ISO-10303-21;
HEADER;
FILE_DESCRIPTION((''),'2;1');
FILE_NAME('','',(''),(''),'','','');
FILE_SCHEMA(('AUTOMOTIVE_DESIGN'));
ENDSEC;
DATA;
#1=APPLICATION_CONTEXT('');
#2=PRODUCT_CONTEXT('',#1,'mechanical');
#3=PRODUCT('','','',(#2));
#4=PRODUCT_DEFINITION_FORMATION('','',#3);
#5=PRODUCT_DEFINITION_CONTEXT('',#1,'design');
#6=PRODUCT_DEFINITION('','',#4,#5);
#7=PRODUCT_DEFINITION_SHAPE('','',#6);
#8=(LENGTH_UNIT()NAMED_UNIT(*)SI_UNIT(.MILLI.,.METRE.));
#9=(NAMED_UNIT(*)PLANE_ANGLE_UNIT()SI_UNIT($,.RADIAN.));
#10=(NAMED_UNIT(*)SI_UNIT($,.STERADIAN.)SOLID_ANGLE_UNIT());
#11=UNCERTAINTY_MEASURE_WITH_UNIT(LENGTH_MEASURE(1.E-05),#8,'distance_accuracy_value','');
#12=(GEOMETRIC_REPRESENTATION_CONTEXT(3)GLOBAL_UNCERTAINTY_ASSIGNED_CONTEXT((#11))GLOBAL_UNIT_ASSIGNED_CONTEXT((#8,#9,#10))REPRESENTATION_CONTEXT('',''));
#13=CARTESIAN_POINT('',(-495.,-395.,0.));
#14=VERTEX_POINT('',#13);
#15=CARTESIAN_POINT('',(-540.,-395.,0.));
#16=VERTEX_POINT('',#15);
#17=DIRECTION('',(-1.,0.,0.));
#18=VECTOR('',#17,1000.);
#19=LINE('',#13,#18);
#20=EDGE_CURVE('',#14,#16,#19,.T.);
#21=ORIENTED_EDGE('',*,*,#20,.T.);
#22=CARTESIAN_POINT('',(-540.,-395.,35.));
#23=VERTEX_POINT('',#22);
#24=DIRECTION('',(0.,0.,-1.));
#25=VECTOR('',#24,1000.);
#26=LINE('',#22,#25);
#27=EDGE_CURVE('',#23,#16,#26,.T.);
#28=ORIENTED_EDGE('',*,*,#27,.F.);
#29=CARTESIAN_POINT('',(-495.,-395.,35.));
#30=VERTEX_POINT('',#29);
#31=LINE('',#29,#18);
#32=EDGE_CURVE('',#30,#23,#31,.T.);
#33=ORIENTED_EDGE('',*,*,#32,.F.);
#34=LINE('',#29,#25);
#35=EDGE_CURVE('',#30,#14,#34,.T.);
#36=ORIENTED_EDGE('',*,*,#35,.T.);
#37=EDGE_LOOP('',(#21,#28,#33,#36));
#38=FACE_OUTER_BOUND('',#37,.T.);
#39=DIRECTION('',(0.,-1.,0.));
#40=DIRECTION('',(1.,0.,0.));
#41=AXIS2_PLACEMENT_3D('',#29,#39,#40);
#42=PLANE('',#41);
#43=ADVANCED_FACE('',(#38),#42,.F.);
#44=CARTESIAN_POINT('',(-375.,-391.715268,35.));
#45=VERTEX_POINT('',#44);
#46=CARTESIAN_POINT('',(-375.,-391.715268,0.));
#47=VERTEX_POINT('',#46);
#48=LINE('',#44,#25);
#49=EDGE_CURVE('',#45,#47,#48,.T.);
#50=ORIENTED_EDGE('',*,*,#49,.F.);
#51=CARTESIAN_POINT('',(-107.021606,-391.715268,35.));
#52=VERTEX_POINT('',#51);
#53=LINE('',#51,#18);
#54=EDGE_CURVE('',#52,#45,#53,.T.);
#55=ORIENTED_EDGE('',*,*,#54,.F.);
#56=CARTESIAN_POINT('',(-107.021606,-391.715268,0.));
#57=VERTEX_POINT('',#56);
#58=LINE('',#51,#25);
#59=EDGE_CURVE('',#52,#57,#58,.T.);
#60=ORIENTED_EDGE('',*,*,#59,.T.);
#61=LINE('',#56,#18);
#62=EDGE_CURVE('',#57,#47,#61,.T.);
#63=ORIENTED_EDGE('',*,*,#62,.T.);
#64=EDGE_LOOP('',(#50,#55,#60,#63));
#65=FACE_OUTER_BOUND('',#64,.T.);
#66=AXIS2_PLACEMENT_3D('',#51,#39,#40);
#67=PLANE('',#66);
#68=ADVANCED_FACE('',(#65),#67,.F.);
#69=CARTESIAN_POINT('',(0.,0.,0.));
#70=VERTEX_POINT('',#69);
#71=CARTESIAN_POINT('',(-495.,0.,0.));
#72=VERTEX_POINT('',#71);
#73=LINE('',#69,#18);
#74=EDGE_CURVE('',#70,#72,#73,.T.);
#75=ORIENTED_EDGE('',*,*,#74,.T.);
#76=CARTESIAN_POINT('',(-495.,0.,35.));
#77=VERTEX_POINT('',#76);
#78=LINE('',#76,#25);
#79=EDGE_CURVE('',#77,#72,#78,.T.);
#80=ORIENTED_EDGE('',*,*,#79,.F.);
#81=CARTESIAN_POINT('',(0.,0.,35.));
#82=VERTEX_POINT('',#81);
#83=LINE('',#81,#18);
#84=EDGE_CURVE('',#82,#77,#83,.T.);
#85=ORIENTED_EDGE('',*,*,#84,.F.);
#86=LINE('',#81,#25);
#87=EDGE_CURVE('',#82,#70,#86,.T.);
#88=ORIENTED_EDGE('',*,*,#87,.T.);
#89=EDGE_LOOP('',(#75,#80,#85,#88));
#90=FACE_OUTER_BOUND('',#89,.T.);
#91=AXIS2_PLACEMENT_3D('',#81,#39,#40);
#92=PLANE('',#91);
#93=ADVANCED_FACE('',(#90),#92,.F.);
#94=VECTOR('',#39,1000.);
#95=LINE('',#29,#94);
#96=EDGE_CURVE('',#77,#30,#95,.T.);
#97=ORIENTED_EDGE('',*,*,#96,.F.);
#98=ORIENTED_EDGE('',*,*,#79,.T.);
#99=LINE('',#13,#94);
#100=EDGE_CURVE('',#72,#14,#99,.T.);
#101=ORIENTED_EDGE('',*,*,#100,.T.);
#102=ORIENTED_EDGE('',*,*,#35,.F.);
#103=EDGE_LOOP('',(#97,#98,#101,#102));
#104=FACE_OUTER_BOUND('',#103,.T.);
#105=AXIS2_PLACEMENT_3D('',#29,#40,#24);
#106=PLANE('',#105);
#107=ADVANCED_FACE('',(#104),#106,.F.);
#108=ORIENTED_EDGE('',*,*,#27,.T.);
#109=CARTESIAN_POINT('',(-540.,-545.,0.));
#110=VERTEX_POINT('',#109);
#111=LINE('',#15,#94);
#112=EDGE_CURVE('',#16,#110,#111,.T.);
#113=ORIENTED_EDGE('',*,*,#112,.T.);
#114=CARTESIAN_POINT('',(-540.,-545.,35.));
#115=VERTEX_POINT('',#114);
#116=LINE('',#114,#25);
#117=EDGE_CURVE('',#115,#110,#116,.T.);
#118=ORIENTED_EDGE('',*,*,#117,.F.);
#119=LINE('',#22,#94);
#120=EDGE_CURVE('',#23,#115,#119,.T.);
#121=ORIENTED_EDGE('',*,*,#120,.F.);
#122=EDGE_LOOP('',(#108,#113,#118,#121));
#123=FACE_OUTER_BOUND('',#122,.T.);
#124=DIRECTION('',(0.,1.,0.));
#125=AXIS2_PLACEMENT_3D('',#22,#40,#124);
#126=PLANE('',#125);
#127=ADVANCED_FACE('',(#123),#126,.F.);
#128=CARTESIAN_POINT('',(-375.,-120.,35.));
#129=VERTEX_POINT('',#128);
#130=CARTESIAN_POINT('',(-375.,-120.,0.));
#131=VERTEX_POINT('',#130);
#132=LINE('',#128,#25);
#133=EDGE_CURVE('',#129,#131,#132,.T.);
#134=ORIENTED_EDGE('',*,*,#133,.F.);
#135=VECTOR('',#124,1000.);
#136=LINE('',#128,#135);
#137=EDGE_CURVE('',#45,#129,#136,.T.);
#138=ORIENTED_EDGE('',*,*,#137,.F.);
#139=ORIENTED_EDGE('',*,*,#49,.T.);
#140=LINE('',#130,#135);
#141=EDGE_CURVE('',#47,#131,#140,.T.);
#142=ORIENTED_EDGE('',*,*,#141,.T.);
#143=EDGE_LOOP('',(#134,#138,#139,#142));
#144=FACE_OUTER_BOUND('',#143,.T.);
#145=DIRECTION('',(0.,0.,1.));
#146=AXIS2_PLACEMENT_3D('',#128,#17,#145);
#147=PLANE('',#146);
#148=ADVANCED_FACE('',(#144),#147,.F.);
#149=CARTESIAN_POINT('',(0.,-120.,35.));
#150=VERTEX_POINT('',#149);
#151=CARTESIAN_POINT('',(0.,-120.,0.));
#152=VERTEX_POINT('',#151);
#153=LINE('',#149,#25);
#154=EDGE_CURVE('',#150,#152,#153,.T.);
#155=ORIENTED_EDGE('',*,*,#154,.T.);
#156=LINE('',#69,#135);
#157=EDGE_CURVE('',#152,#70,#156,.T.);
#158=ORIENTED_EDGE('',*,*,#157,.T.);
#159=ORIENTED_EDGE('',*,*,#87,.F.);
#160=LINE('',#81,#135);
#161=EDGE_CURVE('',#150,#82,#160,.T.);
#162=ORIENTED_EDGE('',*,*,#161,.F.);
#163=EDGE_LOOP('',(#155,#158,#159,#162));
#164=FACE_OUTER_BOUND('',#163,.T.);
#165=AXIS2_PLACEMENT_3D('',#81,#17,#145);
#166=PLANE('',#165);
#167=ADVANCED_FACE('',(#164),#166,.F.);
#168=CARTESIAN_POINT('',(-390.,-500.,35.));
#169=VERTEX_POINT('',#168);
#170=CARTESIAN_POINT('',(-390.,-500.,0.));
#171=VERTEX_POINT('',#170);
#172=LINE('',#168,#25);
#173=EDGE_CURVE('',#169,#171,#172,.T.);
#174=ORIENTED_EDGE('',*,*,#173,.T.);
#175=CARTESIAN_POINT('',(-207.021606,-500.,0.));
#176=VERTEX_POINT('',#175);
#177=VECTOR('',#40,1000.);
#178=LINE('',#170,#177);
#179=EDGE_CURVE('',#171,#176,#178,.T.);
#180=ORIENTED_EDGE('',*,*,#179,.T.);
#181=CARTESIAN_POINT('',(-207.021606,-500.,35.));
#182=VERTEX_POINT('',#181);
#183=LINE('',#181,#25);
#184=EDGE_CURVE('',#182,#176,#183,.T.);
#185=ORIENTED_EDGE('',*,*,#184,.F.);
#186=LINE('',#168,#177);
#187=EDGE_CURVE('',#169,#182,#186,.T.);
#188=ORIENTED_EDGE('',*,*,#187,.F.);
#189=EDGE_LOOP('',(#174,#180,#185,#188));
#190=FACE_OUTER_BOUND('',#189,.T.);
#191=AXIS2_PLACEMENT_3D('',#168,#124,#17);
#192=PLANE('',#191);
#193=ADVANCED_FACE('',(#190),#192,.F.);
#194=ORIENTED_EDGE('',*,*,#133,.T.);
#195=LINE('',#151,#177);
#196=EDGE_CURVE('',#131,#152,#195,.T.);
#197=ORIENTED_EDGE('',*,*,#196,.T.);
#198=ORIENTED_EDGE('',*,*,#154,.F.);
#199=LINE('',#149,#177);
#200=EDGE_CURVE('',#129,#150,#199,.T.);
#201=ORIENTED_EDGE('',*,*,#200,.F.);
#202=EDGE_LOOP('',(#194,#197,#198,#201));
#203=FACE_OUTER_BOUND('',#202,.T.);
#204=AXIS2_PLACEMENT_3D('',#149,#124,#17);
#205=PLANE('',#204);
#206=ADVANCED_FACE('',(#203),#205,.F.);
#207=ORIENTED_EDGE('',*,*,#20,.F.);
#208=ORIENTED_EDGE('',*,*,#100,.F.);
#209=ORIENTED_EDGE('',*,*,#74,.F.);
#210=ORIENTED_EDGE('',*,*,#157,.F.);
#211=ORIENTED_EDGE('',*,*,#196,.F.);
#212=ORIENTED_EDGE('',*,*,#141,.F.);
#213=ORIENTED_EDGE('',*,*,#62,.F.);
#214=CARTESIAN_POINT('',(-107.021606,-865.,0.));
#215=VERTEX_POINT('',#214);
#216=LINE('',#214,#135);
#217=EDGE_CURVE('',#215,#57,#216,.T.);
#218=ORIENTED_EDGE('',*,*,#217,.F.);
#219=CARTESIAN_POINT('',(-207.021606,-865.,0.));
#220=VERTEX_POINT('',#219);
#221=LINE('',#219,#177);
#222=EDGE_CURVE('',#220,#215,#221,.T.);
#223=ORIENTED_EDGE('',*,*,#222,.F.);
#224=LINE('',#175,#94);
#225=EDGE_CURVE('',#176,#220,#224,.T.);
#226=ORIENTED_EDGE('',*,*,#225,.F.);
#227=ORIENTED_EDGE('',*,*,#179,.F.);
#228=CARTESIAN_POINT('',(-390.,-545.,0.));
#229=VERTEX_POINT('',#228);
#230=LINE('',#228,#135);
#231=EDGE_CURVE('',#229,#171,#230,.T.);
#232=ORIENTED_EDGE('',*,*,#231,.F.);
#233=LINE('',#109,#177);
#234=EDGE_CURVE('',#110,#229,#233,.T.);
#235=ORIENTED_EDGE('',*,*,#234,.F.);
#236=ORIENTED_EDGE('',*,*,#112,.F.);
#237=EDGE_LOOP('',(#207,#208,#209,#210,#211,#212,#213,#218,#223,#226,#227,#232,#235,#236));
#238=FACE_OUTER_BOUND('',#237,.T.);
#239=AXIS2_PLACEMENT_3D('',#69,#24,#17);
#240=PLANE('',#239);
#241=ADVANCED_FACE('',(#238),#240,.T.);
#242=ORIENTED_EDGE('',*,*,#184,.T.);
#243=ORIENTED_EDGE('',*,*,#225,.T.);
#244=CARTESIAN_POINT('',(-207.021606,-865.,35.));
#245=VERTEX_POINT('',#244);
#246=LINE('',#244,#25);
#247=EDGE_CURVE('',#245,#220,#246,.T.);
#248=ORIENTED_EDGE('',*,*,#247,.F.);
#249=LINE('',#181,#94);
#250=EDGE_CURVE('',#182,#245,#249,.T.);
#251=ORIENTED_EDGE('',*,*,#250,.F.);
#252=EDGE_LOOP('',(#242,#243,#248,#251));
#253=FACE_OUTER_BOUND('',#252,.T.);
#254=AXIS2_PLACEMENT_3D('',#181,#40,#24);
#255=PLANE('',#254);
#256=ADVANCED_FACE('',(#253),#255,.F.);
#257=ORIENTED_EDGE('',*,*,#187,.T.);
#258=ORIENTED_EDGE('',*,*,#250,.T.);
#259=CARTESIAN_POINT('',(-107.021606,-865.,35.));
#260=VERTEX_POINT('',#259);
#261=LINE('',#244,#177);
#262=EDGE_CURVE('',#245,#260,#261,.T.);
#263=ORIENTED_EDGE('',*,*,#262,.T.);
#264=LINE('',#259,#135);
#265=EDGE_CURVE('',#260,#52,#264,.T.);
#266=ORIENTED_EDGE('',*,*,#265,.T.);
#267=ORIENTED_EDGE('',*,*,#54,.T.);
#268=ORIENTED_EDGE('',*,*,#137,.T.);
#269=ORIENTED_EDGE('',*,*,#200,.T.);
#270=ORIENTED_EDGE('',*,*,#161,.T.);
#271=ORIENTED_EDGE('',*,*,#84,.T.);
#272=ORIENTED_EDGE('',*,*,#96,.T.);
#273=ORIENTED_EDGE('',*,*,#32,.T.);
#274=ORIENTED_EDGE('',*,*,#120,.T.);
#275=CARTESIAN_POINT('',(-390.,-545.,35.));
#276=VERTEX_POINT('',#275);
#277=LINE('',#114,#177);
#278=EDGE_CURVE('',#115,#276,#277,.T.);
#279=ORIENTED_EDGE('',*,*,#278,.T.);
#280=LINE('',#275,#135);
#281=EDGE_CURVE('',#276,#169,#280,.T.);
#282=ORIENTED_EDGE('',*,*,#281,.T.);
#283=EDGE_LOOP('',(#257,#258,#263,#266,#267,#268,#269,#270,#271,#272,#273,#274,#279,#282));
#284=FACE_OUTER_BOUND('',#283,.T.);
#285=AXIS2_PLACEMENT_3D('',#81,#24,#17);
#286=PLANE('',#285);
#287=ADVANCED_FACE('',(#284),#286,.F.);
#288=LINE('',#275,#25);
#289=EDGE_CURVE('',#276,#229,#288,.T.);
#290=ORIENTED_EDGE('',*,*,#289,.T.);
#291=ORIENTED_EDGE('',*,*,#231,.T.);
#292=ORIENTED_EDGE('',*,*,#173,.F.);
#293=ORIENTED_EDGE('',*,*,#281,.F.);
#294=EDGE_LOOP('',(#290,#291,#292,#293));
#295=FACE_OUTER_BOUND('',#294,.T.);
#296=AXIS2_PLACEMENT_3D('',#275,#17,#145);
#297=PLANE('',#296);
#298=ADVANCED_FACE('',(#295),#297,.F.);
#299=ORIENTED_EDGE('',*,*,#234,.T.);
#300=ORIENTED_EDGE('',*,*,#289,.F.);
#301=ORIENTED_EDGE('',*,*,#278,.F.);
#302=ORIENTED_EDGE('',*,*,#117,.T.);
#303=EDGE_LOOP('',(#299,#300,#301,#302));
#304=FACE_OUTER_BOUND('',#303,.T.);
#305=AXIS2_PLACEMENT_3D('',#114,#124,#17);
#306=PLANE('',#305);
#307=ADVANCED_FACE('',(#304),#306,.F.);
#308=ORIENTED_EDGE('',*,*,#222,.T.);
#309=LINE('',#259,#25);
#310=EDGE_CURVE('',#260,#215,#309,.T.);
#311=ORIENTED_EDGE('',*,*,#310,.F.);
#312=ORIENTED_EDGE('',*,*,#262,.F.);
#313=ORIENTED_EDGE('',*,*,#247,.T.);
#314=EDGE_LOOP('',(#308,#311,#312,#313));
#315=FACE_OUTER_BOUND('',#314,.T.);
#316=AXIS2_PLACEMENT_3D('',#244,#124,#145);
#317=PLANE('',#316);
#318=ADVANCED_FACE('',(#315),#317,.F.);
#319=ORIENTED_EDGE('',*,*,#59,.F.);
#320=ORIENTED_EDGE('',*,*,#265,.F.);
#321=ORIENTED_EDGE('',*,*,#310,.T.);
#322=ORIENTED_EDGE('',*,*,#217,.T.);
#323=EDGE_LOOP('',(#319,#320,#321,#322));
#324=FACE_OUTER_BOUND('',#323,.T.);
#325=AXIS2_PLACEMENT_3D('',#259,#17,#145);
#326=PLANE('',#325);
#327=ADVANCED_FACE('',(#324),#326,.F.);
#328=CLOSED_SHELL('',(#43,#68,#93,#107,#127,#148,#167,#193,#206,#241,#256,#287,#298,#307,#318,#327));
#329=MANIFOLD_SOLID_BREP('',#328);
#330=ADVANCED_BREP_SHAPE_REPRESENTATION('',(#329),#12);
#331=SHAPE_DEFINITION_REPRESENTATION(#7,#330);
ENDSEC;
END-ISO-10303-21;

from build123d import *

# Parameters (mm, degrees)
BOSS_EXTRUDE1_DEPTH = 35


with BuildPart() as part:
    # Sketch1 → Boss-Extrude1 (new body)
    with BuildSketch(Plane.XY):
        Polygon((-495, -395), (-495, 0), (0, 0), (0, -120), (-375, -120), (-375, -391.71526804), (-107.021605816, -391.71526804), (-107.021605816, -865), (-207.021605816, -865), (-207.021605816, -500), (-390, -500), (-390, -545), (-540, -545), (-540, -395), align=None)
    extrude(amount=BOSS_EXTRUDE1_DEPTH)


solid = part.part
